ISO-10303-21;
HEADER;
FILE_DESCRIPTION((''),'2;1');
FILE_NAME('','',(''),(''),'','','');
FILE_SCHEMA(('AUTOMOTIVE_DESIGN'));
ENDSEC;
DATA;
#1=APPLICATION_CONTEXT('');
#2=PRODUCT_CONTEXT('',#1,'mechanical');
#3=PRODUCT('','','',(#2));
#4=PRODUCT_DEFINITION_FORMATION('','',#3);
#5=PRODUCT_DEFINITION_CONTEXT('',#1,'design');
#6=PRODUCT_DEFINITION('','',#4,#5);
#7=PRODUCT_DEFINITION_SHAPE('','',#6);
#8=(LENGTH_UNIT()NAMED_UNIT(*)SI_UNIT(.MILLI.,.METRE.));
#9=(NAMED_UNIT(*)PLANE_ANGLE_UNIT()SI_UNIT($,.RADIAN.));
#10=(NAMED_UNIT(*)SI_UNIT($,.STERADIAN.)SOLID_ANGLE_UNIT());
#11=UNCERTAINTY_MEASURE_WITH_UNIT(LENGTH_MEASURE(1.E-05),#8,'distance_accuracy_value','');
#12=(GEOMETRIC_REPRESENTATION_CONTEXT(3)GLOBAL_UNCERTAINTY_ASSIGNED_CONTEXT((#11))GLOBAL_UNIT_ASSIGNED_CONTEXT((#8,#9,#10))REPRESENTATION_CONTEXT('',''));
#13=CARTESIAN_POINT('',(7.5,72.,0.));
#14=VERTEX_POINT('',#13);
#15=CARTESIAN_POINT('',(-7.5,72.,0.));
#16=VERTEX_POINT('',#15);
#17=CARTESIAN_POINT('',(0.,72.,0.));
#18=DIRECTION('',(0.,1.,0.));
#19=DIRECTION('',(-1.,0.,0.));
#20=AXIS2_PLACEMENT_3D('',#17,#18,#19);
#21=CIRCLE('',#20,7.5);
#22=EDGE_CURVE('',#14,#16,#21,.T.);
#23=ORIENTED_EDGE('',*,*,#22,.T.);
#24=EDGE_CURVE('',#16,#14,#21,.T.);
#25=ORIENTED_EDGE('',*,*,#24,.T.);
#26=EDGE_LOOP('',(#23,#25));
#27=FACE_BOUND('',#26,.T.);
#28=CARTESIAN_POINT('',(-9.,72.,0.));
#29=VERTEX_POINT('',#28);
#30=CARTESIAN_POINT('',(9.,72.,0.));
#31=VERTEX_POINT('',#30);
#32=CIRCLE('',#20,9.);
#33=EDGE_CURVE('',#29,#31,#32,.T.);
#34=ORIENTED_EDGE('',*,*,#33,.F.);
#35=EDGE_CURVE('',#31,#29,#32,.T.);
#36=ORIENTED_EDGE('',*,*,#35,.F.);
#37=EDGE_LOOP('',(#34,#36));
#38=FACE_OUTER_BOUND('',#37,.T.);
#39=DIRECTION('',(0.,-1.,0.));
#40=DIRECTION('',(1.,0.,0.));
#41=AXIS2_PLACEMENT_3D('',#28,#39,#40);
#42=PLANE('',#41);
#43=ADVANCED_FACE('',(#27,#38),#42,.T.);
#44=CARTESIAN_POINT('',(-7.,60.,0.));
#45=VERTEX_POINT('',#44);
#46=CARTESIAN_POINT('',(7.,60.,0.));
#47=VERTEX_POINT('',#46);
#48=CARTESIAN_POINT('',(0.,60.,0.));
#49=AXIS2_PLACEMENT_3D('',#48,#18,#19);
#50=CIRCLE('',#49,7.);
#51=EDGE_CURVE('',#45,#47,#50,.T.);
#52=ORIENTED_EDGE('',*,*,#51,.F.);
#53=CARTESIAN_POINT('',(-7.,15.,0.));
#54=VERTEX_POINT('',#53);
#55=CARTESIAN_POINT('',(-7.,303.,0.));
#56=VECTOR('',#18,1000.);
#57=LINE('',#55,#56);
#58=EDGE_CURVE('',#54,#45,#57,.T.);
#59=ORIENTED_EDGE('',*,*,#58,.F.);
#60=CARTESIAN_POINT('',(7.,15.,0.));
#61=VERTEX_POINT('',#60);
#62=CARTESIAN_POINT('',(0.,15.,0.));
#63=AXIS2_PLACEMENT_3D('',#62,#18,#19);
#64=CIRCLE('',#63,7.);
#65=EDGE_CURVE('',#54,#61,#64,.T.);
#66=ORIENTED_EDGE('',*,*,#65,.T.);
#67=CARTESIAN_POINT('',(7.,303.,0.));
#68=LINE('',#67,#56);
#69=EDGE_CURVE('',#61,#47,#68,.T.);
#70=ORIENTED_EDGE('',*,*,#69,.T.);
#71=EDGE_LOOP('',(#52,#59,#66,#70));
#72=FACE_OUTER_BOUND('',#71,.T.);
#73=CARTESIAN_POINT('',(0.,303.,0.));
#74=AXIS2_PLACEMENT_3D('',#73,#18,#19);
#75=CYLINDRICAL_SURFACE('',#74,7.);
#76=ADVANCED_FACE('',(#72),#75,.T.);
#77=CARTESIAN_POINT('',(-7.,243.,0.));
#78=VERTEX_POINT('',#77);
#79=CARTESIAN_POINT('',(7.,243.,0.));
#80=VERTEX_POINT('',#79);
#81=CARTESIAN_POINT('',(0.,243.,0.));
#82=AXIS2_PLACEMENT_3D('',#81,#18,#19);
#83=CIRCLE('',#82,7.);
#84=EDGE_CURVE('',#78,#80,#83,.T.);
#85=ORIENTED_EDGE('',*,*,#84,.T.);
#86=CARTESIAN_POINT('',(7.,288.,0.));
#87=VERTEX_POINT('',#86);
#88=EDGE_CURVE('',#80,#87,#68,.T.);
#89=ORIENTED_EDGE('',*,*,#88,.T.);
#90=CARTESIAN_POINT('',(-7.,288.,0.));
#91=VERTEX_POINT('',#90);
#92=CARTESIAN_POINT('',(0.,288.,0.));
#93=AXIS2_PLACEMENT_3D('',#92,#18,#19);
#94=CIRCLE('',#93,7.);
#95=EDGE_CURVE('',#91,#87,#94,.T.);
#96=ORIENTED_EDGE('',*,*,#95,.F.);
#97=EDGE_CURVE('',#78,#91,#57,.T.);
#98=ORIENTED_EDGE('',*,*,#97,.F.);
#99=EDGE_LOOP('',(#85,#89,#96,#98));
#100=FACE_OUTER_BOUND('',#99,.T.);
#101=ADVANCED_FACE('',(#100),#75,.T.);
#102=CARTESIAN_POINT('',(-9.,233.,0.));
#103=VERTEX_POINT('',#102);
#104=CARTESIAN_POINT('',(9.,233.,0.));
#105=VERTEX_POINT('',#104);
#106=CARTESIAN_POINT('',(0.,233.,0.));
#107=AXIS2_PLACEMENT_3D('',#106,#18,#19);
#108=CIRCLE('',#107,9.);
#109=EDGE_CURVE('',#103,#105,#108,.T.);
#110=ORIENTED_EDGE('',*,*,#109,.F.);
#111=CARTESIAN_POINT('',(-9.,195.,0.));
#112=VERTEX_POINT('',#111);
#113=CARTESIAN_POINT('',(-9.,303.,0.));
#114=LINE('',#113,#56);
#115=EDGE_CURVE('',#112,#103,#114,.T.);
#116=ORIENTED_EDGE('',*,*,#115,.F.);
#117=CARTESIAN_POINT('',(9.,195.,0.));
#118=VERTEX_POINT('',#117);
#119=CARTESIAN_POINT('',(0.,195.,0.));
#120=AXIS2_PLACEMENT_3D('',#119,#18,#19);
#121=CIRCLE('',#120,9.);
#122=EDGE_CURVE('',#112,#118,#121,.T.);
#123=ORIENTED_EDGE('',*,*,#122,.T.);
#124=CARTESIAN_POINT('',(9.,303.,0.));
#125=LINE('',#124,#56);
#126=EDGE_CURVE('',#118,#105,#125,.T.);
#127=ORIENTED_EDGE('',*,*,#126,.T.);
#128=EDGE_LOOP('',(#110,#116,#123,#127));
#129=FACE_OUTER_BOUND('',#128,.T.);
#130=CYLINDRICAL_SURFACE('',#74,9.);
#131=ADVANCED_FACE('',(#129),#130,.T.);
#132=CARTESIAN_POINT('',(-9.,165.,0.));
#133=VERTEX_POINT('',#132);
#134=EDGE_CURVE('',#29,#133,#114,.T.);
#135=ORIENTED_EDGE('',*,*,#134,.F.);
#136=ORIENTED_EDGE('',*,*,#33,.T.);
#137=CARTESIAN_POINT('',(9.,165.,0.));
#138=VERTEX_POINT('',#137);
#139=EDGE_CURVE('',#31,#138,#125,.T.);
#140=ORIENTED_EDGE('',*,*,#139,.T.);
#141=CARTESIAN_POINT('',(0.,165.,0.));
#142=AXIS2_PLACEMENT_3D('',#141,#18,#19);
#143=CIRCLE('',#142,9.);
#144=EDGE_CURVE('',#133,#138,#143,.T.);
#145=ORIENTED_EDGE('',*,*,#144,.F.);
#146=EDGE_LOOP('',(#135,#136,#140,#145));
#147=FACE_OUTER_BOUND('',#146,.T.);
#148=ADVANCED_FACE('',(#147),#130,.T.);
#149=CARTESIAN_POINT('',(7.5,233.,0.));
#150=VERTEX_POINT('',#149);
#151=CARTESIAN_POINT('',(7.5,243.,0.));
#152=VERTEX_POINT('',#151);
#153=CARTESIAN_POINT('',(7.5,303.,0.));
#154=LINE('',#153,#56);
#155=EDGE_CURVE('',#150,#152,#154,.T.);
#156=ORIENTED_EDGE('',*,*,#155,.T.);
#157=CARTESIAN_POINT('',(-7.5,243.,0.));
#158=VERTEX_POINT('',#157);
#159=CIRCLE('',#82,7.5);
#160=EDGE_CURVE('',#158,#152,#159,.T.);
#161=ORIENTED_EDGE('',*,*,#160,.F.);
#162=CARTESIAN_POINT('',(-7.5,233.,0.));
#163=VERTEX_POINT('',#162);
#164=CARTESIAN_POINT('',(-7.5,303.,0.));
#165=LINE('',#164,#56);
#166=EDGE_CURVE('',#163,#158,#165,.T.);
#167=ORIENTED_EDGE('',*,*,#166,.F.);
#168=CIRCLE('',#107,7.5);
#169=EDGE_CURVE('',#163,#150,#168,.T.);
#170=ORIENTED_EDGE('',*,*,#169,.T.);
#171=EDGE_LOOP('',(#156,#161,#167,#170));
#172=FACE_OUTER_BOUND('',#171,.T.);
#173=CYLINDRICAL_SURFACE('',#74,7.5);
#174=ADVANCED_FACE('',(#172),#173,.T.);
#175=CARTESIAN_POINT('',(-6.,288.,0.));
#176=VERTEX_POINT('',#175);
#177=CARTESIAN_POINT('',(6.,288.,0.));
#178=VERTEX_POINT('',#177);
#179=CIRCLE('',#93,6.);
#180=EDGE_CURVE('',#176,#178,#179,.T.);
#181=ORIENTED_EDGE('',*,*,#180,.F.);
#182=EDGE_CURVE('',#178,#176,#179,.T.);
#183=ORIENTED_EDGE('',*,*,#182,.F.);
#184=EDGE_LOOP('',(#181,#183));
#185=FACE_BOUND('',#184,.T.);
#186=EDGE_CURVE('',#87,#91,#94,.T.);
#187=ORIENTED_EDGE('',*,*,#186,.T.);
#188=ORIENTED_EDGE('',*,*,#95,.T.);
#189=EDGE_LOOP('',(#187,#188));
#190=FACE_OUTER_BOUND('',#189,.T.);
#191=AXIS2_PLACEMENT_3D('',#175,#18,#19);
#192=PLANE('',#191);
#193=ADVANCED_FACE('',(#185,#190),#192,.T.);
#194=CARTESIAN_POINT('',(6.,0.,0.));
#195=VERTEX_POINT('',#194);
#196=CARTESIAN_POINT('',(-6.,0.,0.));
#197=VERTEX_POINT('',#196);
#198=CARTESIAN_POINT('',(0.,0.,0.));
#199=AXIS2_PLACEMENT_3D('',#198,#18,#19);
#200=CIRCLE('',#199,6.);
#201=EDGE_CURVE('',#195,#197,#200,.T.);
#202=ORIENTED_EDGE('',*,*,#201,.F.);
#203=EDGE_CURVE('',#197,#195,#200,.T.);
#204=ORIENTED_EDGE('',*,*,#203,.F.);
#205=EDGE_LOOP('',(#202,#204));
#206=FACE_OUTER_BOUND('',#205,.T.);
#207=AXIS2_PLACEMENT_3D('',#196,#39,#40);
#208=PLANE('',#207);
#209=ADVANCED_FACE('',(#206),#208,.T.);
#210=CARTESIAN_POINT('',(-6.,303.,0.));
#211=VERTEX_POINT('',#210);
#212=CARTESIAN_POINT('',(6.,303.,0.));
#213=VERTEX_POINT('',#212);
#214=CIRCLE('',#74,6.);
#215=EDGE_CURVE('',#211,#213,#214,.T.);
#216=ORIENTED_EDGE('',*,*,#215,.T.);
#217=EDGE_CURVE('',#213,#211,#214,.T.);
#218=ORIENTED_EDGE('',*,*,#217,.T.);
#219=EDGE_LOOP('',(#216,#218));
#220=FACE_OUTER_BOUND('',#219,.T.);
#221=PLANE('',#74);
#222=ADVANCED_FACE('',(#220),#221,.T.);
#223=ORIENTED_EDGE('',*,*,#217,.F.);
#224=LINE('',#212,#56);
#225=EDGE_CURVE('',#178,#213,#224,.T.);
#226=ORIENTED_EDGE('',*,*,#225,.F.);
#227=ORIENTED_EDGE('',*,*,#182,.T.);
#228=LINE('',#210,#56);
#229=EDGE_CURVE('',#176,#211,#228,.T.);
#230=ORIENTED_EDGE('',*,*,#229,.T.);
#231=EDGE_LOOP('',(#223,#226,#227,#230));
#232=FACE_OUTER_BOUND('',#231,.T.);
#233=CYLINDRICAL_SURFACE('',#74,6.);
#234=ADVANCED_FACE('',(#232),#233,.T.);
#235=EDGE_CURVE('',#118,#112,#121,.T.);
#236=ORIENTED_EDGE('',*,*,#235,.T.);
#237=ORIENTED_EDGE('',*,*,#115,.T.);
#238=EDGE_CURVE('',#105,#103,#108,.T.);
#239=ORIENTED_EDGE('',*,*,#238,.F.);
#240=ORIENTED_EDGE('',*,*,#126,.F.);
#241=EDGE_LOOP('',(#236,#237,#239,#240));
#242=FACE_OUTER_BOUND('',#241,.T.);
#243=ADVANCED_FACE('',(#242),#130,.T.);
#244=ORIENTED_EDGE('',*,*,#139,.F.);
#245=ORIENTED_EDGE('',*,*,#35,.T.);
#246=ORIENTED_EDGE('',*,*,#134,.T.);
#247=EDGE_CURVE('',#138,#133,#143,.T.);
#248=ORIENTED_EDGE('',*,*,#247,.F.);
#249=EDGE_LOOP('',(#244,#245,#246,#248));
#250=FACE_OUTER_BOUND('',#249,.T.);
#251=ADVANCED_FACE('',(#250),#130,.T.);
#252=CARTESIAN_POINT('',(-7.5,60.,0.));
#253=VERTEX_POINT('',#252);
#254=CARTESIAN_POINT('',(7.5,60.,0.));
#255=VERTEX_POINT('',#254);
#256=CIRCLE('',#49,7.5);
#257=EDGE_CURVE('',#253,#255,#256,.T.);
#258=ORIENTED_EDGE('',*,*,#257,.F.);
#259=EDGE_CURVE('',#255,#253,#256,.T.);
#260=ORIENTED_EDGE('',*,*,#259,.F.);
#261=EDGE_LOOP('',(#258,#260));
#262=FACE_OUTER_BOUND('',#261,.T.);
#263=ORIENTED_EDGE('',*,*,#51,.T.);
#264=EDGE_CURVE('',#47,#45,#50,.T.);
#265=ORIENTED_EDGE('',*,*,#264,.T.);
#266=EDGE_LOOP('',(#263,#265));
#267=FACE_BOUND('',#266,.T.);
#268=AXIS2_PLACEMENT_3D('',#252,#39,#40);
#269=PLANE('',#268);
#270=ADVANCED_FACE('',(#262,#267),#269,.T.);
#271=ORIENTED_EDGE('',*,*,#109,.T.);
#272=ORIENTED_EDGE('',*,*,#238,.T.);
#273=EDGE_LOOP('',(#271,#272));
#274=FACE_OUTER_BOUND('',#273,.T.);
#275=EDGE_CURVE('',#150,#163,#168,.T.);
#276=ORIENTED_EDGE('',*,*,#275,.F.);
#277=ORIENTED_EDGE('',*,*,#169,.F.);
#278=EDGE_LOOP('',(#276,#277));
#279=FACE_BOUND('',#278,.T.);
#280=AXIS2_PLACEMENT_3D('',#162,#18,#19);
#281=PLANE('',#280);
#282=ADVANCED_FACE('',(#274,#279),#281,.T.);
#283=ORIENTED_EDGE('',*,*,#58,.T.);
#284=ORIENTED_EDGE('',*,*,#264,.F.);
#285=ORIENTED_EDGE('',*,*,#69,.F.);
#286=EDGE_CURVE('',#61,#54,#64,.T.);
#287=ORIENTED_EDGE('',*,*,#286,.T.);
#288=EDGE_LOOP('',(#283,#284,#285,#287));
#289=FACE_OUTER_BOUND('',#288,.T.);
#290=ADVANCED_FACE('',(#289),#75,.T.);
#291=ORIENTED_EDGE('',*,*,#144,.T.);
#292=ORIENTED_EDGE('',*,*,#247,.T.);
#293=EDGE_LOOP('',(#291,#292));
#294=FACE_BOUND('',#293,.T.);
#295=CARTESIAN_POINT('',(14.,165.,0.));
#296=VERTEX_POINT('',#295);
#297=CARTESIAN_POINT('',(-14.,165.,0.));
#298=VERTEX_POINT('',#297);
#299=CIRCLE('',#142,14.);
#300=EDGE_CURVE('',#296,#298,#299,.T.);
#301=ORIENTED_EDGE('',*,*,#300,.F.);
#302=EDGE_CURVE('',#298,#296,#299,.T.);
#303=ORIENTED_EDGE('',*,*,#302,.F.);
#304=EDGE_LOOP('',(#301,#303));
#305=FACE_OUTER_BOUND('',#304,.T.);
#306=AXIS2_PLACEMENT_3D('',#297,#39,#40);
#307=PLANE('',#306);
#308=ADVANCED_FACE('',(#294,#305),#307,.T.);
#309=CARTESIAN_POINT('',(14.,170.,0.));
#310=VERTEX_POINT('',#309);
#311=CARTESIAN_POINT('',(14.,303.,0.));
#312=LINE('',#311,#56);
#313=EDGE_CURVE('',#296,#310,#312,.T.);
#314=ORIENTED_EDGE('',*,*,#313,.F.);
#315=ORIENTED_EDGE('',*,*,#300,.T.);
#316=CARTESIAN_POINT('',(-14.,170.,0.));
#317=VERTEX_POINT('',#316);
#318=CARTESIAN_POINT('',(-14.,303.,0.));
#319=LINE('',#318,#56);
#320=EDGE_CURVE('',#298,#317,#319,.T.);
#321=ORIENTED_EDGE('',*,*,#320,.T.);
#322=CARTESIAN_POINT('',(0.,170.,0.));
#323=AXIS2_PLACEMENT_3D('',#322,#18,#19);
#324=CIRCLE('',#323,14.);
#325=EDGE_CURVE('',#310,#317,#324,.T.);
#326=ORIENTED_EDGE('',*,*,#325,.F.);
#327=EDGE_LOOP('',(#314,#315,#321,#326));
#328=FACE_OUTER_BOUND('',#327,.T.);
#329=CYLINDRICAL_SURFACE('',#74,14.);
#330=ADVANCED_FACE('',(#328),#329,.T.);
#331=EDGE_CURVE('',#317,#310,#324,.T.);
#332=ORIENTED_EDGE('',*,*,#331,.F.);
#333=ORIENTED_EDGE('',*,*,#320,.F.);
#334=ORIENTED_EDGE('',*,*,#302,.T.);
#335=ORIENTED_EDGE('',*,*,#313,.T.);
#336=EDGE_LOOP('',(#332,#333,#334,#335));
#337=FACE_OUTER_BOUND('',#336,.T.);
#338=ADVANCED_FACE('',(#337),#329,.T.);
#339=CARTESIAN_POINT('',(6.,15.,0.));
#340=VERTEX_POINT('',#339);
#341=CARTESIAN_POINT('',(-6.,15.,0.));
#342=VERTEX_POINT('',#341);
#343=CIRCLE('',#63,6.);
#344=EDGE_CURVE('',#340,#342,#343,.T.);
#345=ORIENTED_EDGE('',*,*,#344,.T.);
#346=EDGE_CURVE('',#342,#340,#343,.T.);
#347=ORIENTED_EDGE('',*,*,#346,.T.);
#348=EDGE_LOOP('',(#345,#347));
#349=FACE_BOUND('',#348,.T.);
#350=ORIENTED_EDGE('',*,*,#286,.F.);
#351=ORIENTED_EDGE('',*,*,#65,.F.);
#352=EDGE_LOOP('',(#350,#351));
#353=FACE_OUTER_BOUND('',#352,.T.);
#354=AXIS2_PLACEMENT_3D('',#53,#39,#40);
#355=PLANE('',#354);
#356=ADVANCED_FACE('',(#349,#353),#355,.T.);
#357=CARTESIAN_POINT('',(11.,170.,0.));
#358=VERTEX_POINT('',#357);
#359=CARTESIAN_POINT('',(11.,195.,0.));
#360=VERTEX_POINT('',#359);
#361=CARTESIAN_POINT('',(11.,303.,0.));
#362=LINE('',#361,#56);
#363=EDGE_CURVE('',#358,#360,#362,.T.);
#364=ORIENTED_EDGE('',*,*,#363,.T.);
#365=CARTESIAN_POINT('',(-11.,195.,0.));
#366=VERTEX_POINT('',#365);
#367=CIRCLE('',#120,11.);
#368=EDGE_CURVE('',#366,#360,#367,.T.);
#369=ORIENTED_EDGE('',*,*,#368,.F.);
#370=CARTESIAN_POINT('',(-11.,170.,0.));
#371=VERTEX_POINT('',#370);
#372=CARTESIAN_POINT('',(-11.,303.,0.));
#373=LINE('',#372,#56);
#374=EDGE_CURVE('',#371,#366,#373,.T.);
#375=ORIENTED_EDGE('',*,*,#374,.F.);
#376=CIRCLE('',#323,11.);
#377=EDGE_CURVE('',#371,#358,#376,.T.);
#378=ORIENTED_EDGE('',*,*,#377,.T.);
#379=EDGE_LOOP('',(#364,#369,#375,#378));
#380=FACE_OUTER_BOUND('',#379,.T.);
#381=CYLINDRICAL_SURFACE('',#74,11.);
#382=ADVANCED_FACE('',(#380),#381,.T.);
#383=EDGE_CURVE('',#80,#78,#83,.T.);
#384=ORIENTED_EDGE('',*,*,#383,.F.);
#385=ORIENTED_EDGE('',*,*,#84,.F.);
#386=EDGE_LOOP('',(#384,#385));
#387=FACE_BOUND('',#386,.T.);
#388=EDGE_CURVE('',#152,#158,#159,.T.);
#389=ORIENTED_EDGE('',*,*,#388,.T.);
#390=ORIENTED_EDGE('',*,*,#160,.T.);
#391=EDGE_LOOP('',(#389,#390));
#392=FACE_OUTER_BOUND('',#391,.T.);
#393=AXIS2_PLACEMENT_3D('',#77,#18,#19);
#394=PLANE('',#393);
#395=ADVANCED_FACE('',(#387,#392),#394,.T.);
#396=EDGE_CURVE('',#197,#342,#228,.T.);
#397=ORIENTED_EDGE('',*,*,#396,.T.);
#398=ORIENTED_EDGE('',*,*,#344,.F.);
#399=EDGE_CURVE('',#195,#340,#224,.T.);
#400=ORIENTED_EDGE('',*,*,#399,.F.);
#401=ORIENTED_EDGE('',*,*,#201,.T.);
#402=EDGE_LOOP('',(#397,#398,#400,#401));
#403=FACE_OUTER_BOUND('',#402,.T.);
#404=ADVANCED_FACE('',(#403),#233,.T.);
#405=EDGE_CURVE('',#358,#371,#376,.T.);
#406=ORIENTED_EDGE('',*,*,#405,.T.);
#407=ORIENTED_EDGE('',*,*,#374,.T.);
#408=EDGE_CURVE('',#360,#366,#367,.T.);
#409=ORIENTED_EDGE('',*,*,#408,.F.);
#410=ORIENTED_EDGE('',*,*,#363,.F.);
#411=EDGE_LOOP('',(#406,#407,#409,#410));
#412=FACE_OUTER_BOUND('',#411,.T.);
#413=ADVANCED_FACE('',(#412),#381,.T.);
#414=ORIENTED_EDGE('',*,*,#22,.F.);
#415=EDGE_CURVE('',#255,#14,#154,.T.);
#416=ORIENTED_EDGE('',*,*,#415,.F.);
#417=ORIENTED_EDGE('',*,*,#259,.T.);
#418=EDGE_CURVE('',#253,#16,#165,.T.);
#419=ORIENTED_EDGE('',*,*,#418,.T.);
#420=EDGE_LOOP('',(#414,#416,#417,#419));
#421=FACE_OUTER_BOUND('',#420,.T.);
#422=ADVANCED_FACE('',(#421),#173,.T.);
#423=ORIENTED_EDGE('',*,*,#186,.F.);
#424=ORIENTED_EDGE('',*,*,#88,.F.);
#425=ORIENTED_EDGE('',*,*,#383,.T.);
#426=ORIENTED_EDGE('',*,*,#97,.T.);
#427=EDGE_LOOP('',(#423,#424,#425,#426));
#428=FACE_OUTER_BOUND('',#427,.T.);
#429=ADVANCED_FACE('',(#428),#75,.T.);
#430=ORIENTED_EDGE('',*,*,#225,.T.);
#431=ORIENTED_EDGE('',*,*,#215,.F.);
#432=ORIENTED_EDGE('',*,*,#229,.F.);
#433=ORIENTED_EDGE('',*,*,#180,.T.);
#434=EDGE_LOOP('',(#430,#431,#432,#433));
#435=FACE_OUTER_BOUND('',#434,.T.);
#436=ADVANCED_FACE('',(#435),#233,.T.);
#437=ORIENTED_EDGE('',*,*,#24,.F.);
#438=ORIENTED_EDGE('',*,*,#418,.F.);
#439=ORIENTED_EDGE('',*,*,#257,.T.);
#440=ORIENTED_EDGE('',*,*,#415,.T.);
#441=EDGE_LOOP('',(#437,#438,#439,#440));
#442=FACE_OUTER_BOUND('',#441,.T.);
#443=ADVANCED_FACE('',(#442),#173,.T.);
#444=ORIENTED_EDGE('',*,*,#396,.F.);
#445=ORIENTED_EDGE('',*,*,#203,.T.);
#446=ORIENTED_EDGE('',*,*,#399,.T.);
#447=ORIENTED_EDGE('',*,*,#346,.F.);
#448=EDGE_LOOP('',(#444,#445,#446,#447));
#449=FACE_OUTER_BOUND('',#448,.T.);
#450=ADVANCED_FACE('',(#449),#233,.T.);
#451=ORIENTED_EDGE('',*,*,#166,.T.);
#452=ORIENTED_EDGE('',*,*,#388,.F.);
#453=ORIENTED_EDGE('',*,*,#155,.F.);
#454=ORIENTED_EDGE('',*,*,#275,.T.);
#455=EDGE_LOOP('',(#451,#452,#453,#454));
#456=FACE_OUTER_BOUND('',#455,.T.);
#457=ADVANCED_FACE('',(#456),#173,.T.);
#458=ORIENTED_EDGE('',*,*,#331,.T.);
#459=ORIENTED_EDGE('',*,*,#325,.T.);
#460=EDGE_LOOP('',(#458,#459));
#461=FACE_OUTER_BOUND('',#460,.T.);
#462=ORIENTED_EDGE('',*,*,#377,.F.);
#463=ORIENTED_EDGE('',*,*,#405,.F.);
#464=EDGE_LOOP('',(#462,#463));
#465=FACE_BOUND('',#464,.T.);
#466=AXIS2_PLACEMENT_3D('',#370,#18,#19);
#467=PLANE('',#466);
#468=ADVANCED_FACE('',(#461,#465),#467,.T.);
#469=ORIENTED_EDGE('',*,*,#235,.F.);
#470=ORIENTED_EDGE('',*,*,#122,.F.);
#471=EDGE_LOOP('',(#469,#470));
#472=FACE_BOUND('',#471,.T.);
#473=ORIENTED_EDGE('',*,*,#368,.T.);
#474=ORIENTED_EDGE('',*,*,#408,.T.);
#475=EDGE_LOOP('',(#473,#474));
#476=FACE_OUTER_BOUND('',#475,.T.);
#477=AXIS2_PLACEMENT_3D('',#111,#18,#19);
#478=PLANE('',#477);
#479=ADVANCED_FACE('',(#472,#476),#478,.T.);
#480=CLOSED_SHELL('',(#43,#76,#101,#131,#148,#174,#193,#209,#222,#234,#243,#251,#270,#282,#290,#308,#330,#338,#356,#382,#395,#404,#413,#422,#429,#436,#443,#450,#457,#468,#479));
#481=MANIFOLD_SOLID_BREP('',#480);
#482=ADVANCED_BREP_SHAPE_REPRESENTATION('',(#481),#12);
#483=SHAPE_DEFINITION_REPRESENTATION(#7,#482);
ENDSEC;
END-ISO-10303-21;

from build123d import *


with BuildPart() as part:
    # Sketch1 → Revolve1 (revolve)
    with BuildSketch(Plane.XY):
        Polygon((0, 303), (-6, 303), (-6, 288), (-7, 288), (-7, 243), (-7.5, 243), (-7.5, 233), (-9, 233), (-9, 195), (-11, 195), (-11, 170), (-14, 170), (-14, 165), (-9, 165), (-9, 72), (-7.5, 72), (-7.5, 60), (-7, 60), (-7, 15), (-6, 15), (-6, 0), (0, 0), align=None)
    revolve(axis=Axis((0, 303, 0), (0, -1, 0)))


solid = part.part
